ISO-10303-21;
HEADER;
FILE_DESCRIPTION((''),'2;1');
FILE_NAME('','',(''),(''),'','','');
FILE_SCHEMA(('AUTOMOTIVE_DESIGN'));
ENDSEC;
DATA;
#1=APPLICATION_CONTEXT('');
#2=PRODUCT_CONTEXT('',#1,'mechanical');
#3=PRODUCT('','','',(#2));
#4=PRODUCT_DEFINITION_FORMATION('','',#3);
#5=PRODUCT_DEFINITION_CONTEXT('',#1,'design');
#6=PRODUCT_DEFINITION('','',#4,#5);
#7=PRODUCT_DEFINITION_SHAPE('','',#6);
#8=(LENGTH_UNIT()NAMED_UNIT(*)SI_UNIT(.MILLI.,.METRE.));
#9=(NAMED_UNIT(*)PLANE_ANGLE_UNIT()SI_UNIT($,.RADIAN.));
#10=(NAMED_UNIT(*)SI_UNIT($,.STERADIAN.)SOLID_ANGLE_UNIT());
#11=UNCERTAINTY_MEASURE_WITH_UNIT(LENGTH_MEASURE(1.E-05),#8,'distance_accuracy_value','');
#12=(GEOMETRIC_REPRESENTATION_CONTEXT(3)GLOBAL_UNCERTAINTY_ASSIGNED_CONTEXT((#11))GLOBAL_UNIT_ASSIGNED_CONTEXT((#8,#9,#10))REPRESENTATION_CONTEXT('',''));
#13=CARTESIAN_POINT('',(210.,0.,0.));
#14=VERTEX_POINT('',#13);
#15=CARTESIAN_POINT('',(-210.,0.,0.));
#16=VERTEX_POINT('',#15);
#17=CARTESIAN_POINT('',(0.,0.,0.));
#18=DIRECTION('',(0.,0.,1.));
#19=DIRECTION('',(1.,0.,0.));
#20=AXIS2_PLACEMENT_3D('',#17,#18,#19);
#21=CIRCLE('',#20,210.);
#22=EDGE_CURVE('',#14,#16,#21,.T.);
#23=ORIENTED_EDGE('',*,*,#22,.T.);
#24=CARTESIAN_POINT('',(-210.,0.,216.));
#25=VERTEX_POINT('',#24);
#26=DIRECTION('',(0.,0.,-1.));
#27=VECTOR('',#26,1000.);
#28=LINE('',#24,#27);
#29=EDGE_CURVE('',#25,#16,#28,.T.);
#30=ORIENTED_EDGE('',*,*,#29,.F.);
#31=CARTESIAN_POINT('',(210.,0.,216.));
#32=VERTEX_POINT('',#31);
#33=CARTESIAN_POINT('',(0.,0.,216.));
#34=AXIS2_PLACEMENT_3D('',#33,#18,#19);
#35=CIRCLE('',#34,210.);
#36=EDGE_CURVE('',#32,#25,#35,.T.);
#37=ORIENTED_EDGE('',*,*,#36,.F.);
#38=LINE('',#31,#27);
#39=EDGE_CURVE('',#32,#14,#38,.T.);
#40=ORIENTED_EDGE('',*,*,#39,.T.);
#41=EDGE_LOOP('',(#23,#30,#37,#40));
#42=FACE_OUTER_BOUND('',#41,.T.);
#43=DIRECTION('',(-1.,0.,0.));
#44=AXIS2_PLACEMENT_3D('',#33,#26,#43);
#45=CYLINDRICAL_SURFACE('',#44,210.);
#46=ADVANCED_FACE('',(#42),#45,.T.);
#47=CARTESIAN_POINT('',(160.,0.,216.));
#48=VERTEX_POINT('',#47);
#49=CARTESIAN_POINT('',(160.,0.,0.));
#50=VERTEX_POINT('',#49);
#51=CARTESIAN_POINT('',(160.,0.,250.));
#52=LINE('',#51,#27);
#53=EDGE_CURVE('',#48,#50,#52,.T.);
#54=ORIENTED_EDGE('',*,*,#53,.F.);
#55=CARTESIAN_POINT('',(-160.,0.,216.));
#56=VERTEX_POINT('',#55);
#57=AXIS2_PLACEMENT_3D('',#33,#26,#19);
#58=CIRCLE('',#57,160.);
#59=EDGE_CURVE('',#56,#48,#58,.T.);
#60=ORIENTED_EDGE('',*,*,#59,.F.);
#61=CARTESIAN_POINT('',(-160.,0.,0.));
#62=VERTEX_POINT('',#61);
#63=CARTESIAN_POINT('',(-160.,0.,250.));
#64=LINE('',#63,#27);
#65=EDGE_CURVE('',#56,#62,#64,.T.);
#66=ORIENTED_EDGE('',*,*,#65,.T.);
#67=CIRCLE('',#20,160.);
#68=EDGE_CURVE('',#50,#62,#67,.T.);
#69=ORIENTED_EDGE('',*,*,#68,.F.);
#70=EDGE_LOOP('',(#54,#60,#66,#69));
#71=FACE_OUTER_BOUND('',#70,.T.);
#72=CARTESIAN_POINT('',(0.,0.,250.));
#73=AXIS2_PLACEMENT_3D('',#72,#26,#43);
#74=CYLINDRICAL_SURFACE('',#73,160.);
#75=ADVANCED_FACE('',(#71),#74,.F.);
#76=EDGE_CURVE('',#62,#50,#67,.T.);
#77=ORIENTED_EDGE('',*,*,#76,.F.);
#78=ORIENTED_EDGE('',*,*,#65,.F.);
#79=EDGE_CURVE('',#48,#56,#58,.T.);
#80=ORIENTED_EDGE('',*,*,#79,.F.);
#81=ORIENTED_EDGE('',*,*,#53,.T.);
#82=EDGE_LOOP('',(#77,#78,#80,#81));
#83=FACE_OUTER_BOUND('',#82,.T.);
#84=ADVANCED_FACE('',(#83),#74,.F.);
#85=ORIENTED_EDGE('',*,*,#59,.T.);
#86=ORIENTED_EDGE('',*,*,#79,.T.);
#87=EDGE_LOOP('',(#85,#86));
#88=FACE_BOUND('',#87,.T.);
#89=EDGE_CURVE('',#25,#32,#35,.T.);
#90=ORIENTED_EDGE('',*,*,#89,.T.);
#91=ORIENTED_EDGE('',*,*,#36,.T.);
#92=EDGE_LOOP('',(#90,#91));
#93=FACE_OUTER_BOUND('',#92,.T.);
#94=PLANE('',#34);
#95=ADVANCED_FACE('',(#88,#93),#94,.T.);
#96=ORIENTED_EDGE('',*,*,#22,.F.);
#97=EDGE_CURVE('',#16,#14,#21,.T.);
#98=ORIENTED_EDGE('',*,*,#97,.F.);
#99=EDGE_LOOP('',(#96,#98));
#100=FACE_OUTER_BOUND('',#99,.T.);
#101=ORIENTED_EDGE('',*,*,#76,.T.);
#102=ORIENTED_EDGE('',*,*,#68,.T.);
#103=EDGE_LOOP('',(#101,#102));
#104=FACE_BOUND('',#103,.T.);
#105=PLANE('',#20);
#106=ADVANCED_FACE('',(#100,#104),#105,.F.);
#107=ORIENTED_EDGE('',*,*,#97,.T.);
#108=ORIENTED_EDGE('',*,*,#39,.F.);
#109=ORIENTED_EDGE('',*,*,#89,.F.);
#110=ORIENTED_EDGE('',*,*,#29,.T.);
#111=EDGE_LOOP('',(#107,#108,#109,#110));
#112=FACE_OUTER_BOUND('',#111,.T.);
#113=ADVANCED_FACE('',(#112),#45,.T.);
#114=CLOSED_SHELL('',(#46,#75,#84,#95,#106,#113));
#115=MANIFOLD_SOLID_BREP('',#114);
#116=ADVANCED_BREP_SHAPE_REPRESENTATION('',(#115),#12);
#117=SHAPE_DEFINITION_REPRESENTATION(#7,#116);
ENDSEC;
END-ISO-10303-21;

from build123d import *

# Parameters (mm, degrees)
SKETCH_1_R          = 210
EXTRUDE_1_DEPTH     = 216
SKETCH_2_R          = 160
CUT_EXTRUDE_1_DEPTH = 250


with BuildPart() as part:
    # 草图1 → 凸台-拉伸1 (new body)
    with BuildSketch(Plane.XY):
        Circle(SKETCH_1_R)
    extrude(amount=EXTRUDE_1_DEPTH)

    # 草图2 → 切除-拉伸1 (cut)
    with BuildSketch(Plane.XY):
        Circle(SKETCH_2_R)
    extrude(amount=CUT_EXTRUDE_1_DEPTH, mode=Mode.SUBTRACT)


solid = part.part
